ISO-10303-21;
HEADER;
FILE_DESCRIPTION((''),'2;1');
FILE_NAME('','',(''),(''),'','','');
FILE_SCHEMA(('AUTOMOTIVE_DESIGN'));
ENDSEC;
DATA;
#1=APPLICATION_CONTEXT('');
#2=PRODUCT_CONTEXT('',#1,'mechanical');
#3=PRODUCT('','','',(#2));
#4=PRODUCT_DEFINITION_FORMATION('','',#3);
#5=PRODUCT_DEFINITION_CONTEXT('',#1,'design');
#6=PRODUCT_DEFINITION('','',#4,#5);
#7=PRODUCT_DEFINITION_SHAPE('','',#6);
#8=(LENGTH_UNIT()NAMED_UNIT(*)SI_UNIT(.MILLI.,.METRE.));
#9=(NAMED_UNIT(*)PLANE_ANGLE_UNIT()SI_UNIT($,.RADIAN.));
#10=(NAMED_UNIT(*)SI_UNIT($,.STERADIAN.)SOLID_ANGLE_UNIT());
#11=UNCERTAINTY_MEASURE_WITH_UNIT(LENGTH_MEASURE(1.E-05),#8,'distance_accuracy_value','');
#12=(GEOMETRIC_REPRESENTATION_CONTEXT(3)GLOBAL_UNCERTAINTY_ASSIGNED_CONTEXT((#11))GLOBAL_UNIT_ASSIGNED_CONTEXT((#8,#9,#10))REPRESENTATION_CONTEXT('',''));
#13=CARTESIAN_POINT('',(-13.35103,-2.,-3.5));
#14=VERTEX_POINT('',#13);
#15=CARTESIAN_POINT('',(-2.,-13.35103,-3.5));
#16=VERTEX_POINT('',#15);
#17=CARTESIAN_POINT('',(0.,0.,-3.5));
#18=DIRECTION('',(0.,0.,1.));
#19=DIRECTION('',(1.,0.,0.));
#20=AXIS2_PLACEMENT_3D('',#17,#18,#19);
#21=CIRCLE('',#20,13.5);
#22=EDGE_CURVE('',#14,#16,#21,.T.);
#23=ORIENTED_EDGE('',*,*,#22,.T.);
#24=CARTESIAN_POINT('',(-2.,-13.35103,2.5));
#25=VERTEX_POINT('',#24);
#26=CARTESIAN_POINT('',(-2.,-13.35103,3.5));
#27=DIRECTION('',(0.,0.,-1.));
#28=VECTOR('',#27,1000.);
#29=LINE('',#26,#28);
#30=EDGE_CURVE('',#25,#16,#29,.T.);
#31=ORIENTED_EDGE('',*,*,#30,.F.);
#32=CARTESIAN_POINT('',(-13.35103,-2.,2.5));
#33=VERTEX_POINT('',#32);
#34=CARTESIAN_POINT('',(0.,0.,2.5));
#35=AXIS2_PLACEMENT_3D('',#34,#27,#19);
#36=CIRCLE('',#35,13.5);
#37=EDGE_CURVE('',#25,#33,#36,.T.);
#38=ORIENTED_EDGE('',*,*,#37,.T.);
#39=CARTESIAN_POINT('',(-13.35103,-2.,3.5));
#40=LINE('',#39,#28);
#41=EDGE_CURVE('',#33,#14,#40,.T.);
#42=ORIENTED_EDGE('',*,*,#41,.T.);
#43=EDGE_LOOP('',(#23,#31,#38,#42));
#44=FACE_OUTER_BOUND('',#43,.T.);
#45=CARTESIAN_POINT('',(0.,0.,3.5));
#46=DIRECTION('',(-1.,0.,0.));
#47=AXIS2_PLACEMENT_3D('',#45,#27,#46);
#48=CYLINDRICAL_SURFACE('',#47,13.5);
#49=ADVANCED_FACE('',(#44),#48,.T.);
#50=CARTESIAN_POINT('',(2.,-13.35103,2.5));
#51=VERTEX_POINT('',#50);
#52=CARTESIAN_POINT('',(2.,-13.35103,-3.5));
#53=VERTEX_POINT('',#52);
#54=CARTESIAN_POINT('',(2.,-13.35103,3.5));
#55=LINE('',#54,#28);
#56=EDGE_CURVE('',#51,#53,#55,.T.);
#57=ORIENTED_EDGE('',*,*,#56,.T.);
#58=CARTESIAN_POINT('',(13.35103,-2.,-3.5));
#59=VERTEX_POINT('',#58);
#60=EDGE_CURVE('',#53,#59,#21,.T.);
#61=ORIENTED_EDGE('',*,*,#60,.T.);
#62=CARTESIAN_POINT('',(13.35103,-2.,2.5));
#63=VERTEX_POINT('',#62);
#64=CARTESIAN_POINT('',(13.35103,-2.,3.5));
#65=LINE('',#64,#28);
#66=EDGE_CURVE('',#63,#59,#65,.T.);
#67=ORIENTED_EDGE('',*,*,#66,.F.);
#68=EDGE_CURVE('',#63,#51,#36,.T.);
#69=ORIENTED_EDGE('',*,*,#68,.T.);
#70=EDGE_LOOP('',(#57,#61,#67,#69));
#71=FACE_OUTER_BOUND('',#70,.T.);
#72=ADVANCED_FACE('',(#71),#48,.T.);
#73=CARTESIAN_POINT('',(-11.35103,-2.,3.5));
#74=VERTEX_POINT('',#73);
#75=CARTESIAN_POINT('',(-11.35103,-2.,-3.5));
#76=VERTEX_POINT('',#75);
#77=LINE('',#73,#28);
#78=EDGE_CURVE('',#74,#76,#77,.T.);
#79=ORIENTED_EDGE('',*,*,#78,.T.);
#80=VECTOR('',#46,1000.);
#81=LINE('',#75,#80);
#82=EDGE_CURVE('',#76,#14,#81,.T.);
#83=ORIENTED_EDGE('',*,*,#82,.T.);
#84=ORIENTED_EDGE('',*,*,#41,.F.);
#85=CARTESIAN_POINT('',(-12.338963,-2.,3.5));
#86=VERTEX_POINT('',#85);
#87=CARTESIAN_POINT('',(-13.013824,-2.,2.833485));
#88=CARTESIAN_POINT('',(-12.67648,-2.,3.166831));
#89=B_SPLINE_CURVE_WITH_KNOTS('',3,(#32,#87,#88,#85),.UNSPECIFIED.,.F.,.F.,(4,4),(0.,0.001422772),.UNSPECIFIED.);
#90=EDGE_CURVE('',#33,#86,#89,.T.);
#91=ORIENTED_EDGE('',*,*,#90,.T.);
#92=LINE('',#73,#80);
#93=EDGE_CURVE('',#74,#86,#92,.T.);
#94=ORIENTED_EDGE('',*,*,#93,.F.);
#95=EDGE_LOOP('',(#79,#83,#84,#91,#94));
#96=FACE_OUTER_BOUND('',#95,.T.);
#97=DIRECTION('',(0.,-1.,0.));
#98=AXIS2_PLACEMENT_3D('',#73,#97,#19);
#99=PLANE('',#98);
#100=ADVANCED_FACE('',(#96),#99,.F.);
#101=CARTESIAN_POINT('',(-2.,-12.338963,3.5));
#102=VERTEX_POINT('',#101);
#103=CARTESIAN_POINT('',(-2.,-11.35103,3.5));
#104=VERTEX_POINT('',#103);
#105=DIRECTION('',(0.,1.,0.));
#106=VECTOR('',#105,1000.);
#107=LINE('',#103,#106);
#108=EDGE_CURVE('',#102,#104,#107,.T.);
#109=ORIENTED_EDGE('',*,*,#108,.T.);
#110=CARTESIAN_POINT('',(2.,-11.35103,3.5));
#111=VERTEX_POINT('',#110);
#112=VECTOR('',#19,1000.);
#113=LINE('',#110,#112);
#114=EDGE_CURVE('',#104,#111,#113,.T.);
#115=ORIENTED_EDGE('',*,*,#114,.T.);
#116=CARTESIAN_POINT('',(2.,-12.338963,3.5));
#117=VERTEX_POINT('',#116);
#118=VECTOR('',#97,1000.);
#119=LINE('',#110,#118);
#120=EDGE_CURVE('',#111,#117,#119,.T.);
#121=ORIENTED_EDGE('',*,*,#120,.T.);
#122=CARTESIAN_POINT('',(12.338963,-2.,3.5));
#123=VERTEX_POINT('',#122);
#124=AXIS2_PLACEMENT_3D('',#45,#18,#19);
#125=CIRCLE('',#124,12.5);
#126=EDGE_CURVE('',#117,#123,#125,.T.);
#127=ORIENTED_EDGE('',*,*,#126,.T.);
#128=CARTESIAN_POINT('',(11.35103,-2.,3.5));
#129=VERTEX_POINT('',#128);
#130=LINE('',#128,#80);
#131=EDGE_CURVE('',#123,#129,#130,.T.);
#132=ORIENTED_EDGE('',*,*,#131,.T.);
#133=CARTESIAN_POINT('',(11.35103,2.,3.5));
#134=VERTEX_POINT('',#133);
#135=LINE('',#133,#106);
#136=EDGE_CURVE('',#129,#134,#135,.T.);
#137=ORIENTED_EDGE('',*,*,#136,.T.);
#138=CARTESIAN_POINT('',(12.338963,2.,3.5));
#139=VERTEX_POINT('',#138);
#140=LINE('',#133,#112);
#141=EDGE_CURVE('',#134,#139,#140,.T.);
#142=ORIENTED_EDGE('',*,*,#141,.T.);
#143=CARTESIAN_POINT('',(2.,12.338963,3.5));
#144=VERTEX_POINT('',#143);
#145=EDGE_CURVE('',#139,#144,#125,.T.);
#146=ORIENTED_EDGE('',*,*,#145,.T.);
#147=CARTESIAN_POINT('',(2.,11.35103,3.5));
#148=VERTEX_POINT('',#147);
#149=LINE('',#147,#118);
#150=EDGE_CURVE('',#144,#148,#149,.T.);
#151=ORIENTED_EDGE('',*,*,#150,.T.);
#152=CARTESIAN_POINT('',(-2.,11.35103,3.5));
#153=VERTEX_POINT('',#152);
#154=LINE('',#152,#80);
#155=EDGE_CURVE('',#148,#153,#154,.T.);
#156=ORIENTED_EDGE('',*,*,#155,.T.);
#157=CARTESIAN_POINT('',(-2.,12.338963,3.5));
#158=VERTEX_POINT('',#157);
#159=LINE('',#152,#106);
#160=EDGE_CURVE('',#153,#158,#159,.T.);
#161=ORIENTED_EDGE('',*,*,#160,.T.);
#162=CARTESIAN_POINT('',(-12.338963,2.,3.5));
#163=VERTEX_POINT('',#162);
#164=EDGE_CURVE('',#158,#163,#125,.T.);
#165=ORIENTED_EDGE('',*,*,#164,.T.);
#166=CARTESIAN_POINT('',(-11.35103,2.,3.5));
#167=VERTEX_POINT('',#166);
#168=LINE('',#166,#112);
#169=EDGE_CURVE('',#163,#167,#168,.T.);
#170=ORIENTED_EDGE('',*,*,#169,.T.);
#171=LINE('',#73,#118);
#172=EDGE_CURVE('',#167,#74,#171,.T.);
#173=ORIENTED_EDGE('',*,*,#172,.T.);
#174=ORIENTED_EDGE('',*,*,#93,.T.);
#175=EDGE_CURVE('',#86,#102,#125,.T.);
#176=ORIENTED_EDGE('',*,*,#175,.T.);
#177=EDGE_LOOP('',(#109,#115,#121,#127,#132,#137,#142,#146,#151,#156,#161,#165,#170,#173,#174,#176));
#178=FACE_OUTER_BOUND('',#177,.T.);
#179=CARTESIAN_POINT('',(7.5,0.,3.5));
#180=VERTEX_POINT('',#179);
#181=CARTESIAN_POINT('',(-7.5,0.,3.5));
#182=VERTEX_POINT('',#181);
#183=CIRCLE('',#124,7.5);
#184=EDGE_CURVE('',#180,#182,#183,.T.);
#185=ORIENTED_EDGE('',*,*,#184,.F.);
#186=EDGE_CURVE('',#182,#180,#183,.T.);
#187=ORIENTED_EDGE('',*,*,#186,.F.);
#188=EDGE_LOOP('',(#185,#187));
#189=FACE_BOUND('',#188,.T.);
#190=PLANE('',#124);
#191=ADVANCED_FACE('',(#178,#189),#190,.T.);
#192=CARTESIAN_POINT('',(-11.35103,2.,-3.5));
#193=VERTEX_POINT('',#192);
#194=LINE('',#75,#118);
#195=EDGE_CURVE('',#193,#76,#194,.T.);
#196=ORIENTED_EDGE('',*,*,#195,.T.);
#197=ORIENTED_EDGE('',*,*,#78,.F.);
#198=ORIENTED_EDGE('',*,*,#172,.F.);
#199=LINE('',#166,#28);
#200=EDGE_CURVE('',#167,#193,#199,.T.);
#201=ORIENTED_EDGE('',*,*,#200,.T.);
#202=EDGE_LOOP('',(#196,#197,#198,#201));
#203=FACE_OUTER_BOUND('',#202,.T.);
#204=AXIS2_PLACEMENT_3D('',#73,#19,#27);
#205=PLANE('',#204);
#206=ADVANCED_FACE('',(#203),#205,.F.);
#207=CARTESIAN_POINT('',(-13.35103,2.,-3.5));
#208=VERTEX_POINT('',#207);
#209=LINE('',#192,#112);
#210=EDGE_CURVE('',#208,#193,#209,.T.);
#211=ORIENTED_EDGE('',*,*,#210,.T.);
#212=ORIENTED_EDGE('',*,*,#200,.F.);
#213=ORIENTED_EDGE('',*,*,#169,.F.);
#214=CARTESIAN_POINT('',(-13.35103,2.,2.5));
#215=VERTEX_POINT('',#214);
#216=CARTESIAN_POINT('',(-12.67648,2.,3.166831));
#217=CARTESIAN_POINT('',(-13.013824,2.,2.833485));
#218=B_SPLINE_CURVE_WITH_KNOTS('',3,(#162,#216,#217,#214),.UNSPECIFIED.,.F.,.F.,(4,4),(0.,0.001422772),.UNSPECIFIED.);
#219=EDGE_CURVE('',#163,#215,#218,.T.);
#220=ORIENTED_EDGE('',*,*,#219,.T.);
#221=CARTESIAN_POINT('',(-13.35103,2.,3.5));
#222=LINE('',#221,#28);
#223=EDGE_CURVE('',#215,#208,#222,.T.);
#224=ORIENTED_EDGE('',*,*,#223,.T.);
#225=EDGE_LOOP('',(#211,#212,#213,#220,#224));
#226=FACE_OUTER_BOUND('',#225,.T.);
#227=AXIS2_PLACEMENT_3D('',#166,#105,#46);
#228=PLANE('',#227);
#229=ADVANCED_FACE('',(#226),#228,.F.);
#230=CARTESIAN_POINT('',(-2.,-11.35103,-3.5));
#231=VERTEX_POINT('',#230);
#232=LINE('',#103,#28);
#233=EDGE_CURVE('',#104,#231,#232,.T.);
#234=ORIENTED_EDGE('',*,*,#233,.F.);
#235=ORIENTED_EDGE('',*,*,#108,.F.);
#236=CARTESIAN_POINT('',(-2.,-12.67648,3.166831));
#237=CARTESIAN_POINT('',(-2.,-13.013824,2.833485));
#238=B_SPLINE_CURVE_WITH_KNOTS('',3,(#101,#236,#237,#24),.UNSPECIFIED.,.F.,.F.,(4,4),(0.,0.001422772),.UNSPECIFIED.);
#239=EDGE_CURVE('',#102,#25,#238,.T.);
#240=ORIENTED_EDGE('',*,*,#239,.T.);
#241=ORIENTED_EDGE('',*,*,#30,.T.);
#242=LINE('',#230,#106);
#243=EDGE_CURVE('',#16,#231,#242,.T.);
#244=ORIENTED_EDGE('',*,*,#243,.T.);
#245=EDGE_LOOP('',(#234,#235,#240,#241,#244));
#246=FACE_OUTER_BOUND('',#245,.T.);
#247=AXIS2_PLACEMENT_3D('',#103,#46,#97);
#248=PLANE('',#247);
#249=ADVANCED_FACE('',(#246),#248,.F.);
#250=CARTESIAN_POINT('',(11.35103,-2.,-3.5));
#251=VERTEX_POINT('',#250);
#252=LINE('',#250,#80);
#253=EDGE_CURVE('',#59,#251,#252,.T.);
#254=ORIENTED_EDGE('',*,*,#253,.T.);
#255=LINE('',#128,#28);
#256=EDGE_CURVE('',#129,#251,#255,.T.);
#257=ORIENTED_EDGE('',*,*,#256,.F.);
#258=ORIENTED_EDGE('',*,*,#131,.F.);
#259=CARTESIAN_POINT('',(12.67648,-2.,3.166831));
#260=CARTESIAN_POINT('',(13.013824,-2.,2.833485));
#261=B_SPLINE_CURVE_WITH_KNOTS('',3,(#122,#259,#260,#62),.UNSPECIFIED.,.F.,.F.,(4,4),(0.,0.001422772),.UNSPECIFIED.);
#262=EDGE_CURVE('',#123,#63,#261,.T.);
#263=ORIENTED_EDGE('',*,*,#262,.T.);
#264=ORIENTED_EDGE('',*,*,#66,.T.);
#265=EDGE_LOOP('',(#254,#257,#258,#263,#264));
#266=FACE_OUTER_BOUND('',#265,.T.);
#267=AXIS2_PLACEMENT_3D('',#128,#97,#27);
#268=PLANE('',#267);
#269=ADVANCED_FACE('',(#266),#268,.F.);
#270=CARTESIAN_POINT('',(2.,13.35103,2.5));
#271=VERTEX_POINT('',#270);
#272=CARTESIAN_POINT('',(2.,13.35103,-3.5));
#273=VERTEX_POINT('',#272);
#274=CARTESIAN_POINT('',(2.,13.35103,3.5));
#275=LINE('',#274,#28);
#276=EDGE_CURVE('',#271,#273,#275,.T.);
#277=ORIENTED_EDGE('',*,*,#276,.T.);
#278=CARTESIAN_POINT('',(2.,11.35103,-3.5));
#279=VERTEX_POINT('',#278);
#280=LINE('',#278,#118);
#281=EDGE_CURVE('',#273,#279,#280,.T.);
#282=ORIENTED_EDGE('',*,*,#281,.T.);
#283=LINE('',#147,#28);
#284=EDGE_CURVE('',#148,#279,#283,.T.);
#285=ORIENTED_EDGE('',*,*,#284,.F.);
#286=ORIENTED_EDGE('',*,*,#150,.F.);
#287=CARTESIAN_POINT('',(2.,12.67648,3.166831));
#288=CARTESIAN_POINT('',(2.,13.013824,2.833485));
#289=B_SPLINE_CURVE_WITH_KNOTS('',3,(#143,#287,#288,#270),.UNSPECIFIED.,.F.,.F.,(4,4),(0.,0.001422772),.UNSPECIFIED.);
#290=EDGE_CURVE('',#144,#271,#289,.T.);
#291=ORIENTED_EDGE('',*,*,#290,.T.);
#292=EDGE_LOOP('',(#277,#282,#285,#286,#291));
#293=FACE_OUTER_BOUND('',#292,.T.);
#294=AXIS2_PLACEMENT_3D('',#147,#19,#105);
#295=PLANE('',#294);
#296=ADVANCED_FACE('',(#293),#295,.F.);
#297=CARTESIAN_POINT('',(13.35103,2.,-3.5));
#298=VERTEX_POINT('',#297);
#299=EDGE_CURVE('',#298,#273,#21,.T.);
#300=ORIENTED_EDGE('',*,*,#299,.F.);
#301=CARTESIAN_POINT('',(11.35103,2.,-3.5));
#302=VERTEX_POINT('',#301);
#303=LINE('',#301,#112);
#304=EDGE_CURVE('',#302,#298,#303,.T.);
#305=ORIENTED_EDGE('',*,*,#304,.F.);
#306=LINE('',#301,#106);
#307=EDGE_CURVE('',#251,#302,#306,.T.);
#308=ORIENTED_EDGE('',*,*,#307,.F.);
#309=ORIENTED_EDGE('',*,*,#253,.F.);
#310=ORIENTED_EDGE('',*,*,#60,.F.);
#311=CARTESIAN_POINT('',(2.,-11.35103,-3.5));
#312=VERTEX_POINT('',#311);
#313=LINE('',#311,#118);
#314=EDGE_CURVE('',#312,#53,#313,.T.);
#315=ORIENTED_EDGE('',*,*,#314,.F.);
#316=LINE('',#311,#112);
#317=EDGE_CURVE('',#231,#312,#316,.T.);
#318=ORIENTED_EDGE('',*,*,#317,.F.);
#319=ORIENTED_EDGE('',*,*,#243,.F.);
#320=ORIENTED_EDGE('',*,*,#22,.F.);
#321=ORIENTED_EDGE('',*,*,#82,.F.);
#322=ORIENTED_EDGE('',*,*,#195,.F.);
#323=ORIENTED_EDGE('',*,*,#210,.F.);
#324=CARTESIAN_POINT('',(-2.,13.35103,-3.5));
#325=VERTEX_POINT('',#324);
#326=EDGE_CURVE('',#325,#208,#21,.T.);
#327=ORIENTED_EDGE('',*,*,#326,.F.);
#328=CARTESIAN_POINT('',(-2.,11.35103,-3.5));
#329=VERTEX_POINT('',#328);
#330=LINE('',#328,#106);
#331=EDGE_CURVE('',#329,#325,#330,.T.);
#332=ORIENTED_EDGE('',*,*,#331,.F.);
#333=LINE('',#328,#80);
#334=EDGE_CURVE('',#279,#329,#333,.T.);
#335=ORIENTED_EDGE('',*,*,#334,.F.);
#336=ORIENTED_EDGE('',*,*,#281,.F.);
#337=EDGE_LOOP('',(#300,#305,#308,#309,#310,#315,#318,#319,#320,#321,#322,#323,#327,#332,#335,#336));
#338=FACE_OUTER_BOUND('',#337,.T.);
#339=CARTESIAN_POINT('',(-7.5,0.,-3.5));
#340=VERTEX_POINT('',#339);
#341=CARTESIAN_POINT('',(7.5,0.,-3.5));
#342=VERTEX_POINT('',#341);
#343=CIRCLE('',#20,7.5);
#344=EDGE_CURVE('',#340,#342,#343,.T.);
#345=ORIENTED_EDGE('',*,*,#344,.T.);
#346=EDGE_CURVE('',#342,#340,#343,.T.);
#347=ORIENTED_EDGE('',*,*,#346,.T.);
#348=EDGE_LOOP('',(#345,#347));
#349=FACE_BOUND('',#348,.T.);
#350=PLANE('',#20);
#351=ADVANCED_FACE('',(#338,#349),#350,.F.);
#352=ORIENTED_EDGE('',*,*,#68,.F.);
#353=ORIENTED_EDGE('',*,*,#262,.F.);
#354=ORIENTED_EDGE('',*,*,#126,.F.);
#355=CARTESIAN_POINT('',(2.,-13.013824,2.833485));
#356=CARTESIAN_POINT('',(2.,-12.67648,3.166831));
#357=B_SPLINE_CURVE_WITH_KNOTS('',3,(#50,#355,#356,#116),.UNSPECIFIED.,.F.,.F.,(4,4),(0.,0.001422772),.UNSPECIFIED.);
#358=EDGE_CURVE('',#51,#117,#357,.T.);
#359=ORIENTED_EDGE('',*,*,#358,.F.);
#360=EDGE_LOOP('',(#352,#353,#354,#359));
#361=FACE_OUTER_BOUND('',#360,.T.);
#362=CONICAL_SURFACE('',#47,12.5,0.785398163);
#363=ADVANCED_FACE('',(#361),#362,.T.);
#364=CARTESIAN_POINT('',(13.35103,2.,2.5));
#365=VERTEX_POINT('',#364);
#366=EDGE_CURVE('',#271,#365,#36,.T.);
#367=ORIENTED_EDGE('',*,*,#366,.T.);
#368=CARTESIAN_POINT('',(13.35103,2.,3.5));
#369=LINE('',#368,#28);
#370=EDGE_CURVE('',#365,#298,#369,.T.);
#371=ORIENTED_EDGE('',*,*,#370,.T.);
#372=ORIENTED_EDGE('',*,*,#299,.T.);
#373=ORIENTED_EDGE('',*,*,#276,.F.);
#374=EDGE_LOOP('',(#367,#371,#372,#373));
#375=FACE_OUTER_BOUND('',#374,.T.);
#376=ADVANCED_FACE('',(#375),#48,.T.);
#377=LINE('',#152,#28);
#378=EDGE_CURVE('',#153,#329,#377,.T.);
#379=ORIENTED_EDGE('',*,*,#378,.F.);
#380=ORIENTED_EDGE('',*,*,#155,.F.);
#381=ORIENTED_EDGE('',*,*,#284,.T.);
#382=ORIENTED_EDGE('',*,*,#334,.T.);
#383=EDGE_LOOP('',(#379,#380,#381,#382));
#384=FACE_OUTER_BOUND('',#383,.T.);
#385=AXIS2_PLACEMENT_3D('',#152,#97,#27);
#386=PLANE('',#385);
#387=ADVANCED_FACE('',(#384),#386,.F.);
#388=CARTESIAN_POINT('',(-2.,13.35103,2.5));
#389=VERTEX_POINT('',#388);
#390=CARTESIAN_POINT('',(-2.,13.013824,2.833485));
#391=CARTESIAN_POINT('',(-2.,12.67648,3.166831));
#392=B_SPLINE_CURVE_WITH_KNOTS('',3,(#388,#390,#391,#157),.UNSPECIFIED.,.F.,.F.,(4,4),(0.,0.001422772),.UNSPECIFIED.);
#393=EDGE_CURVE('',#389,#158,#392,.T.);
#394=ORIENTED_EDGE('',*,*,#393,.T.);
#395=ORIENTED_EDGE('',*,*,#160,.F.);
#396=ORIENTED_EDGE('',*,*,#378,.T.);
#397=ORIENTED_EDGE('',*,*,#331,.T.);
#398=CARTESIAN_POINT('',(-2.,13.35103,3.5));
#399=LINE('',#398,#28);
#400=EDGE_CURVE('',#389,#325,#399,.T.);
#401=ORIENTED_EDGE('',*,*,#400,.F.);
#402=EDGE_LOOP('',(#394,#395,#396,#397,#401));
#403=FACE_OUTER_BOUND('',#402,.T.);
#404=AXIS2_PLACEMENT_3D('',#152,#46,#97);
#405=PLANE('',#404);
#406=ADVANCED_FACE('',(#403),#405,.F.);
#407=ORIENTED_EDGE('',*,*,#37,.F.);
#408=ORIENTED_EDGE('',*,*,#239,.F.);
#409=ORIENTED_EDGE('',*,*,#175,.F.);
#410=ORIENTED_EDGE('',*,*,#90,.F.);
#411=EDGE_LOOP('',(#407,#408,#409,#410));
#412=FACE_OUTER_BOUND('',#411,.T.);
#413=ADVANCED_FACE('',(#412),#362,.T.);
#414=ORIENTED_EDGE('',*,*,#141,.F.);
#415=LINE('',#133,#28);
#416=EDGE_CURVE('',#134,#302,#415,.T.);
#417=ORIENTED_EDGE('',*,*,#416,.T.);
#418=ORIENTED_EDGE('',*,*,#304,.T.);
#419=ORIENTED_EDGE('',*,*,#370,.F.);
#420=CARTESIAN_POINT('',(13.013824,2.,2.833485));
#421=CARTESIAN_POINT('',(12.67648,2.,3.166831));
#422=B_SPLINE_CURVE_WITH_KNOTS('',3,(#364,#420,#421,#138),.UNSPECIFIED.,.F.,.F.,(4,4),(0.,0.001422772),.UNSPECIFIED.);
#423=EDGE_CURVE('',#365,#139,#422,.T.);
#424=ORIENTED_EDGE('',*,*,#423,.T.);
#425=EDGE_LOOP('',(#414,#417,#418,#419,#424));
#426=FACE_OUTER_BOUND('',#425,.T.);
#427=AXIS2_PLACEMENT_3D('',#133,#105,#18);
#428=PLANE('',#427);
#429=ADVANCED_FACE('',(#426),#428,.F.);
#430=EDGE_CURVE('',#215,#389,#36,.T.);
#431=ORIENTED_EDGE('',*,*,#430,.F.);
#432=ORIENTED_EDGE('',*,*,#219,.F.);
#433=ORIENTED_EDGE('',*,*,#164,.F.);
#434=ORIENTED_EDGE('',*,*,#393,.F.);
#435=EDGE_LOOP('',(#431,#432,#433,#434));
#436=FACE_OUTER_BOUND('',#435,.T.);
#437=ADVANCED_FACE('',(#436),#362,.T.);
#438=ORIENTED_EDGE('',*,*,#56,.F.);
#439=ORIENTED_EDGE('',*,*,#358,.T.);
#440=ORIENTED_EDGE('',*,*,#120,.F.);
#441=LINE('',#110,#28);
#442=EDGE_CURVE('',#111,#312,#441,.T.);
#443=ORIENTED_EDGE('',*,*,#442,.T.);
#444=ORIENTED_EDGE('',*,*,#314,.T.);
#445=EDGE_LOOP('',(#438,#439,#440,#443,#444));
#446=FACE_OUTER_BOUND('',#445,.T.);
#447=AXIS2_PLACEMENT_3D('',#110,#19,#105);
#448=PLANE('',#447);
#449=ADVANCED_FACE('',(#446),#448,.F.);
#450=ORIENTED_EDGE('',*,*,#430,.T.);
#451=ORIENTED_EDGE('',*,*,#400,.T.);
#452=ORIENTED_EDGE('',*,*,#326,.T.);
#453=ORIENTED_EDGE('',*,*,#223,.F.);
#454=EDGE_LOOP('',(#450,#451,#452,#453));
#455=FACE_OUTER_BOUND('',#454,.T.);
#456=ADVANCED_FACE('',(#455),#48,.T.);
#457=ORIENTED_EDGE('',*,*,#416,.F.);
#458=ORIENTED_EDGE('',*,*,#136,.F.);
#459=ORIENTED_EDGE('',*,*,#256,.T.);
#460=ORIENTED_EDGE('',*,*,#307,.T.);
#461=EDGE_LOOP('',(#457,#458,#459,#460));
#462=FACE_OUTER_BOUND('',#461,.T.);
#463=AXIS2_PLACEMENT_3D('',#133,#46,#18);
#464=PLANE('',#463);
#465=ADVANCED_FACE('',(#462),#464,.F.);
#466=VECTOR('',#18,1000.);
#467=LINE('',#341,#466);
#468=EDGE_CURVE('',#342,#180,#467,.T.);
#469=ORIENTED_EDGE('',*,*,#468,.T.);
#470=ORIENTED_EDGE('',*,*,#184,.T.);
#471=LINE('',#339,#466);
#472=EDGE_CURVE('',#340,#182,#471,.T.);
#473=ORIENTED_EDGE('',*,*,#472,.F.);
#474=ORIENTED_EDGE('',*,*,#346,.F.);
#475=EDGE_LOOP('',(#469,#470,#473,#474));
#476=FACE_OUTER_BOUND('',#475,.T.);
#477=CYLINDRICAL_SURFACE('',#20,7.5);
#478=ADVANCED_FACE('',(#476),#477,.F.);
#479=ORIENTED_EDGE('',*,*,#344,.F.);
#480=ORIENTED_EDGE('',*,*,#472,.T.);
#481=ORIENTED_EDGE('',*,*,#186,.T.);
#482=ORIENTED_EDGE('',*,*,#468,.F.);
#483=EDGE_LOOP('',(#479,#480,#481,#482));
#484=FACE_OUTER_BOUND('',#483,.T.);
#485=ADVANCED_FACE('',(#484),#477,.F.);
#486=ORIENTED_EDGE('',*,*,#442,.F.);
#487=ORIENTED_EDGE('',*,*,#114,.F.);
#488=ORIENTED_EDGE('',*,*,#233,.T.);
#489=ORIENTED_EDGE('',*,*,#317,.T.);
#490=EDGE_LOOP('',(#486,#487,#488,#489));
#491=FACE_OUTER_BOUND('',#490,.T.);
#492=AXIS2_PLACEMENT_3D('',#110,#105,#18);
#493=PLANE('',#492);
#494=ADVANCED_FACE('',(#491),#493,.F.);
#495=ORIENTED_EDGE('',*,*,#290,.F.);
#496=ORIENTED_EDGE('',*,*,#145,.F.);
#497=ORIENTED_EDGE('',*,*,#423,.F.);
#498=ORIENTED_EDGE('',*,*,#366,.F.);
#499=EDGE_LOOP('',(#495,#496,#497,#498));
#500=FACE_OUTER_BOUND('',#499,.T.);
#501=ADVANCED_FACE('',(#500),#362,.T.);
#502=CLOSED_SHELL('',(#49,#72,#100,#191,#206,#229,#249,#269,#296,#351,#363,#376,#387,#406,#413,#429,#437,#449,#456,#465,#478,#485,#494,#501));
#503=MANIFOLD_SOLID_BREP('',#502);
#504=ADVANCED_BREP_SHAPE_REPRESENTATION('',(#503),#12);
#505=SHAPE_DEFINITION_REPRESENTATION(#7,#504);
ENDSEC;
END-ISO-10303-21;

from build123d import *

# Parameters (mm, degrees)
NUT_BODY_7MM_DEPTH      = 3.5
BORE_15_DEPTH           = 21.137030566
BORE_15_DEPTH_BACK      = 21.137030566
BORE_SKETCH_15_R        = 7.5
EDGE_CHAMFERS_1X45_SIZE = 1


with BuildPart() as part:
    # Slotted Nut Profile Ø27 → Nut Body 7mm (new, symmetric)
    with BuildSketch(Plane.XY):
        with BuildLine():
            Line((2, 11.351029923), (2, 13.351029923))
            ThreePointArc((2, 13.351029923), (9.545941546, 9.545941546), (13.351029923, 2))
            Line((13.351029923, 2), (11.351029923, 2))
            Line((11.351029923, 2), (11.351029923, -2))
            Line((11.351029923, -2), (13.351029923, -2))
            ThreePointArc((13.351029923, -2), (9.545941546, -9.545941546), (2, -13.351029923))
            Line((2, -13.351029923), (2, -11.351029923))
            Line((2, -11.351029923), (-2, -11.351029923))
            Line((-2, -11.351029923), (-2, -13.351029923))
            ThreePointArc((-2, -13.351029923), (-9.545941546, -9.545941546), (-13.351029923, -2))
            Line((-13.351029923, -2), (-11.351029923, -2))
            Line((-11.351029923, -2), (-11.351029923, 2))
            Line((-11.351029923, 2), (-13.351029923, 2))
            ThreePointArc((-13.351029923, 2), (-9.545941546, 9.545941546), (-2, 13.351029923))
            Line((-2, 13.351029923), (-2, 11.351029923))
            Line((-2, 11.351029923), (2, 11.351029923))
        make_face()
    extrude(amount=NUT_BODY_7MM_DEPTH, both=True)

    # Bore Sketch Ø15 → Bore Ø15 (cut, two sides: drawn at the far end of the back side and taken through both)
    with BuildSketch(Plane.XY.offset(3.5).offset(-BORE_15_DEPTH_BACK)):
        Circle(BORE_SKETCH_15_R)
    extrude(amount=BORE_15_DEPTH + BORE_15_DEPTH_BACK, mode=Mode.SUBTRACT)

    # Edge Chamfers 1x45°
    edge_chamfers_1x45_edges = [part.edges().sort_by_distance(p)[0] for p in [
        (-9.545941546, 9.545941546, 3.5),
        (-9.545941546, -9.545941546, 3.5),
        (9.545941546, -9.545941546, 3.5),
        (9.545941546, 9.545941546, 3.5),
    ]]
    chamfer(edge_chamfers_1x45_edges, length=EDGE_CHAMFERS_1X45_SIZE)


solid = part.part
